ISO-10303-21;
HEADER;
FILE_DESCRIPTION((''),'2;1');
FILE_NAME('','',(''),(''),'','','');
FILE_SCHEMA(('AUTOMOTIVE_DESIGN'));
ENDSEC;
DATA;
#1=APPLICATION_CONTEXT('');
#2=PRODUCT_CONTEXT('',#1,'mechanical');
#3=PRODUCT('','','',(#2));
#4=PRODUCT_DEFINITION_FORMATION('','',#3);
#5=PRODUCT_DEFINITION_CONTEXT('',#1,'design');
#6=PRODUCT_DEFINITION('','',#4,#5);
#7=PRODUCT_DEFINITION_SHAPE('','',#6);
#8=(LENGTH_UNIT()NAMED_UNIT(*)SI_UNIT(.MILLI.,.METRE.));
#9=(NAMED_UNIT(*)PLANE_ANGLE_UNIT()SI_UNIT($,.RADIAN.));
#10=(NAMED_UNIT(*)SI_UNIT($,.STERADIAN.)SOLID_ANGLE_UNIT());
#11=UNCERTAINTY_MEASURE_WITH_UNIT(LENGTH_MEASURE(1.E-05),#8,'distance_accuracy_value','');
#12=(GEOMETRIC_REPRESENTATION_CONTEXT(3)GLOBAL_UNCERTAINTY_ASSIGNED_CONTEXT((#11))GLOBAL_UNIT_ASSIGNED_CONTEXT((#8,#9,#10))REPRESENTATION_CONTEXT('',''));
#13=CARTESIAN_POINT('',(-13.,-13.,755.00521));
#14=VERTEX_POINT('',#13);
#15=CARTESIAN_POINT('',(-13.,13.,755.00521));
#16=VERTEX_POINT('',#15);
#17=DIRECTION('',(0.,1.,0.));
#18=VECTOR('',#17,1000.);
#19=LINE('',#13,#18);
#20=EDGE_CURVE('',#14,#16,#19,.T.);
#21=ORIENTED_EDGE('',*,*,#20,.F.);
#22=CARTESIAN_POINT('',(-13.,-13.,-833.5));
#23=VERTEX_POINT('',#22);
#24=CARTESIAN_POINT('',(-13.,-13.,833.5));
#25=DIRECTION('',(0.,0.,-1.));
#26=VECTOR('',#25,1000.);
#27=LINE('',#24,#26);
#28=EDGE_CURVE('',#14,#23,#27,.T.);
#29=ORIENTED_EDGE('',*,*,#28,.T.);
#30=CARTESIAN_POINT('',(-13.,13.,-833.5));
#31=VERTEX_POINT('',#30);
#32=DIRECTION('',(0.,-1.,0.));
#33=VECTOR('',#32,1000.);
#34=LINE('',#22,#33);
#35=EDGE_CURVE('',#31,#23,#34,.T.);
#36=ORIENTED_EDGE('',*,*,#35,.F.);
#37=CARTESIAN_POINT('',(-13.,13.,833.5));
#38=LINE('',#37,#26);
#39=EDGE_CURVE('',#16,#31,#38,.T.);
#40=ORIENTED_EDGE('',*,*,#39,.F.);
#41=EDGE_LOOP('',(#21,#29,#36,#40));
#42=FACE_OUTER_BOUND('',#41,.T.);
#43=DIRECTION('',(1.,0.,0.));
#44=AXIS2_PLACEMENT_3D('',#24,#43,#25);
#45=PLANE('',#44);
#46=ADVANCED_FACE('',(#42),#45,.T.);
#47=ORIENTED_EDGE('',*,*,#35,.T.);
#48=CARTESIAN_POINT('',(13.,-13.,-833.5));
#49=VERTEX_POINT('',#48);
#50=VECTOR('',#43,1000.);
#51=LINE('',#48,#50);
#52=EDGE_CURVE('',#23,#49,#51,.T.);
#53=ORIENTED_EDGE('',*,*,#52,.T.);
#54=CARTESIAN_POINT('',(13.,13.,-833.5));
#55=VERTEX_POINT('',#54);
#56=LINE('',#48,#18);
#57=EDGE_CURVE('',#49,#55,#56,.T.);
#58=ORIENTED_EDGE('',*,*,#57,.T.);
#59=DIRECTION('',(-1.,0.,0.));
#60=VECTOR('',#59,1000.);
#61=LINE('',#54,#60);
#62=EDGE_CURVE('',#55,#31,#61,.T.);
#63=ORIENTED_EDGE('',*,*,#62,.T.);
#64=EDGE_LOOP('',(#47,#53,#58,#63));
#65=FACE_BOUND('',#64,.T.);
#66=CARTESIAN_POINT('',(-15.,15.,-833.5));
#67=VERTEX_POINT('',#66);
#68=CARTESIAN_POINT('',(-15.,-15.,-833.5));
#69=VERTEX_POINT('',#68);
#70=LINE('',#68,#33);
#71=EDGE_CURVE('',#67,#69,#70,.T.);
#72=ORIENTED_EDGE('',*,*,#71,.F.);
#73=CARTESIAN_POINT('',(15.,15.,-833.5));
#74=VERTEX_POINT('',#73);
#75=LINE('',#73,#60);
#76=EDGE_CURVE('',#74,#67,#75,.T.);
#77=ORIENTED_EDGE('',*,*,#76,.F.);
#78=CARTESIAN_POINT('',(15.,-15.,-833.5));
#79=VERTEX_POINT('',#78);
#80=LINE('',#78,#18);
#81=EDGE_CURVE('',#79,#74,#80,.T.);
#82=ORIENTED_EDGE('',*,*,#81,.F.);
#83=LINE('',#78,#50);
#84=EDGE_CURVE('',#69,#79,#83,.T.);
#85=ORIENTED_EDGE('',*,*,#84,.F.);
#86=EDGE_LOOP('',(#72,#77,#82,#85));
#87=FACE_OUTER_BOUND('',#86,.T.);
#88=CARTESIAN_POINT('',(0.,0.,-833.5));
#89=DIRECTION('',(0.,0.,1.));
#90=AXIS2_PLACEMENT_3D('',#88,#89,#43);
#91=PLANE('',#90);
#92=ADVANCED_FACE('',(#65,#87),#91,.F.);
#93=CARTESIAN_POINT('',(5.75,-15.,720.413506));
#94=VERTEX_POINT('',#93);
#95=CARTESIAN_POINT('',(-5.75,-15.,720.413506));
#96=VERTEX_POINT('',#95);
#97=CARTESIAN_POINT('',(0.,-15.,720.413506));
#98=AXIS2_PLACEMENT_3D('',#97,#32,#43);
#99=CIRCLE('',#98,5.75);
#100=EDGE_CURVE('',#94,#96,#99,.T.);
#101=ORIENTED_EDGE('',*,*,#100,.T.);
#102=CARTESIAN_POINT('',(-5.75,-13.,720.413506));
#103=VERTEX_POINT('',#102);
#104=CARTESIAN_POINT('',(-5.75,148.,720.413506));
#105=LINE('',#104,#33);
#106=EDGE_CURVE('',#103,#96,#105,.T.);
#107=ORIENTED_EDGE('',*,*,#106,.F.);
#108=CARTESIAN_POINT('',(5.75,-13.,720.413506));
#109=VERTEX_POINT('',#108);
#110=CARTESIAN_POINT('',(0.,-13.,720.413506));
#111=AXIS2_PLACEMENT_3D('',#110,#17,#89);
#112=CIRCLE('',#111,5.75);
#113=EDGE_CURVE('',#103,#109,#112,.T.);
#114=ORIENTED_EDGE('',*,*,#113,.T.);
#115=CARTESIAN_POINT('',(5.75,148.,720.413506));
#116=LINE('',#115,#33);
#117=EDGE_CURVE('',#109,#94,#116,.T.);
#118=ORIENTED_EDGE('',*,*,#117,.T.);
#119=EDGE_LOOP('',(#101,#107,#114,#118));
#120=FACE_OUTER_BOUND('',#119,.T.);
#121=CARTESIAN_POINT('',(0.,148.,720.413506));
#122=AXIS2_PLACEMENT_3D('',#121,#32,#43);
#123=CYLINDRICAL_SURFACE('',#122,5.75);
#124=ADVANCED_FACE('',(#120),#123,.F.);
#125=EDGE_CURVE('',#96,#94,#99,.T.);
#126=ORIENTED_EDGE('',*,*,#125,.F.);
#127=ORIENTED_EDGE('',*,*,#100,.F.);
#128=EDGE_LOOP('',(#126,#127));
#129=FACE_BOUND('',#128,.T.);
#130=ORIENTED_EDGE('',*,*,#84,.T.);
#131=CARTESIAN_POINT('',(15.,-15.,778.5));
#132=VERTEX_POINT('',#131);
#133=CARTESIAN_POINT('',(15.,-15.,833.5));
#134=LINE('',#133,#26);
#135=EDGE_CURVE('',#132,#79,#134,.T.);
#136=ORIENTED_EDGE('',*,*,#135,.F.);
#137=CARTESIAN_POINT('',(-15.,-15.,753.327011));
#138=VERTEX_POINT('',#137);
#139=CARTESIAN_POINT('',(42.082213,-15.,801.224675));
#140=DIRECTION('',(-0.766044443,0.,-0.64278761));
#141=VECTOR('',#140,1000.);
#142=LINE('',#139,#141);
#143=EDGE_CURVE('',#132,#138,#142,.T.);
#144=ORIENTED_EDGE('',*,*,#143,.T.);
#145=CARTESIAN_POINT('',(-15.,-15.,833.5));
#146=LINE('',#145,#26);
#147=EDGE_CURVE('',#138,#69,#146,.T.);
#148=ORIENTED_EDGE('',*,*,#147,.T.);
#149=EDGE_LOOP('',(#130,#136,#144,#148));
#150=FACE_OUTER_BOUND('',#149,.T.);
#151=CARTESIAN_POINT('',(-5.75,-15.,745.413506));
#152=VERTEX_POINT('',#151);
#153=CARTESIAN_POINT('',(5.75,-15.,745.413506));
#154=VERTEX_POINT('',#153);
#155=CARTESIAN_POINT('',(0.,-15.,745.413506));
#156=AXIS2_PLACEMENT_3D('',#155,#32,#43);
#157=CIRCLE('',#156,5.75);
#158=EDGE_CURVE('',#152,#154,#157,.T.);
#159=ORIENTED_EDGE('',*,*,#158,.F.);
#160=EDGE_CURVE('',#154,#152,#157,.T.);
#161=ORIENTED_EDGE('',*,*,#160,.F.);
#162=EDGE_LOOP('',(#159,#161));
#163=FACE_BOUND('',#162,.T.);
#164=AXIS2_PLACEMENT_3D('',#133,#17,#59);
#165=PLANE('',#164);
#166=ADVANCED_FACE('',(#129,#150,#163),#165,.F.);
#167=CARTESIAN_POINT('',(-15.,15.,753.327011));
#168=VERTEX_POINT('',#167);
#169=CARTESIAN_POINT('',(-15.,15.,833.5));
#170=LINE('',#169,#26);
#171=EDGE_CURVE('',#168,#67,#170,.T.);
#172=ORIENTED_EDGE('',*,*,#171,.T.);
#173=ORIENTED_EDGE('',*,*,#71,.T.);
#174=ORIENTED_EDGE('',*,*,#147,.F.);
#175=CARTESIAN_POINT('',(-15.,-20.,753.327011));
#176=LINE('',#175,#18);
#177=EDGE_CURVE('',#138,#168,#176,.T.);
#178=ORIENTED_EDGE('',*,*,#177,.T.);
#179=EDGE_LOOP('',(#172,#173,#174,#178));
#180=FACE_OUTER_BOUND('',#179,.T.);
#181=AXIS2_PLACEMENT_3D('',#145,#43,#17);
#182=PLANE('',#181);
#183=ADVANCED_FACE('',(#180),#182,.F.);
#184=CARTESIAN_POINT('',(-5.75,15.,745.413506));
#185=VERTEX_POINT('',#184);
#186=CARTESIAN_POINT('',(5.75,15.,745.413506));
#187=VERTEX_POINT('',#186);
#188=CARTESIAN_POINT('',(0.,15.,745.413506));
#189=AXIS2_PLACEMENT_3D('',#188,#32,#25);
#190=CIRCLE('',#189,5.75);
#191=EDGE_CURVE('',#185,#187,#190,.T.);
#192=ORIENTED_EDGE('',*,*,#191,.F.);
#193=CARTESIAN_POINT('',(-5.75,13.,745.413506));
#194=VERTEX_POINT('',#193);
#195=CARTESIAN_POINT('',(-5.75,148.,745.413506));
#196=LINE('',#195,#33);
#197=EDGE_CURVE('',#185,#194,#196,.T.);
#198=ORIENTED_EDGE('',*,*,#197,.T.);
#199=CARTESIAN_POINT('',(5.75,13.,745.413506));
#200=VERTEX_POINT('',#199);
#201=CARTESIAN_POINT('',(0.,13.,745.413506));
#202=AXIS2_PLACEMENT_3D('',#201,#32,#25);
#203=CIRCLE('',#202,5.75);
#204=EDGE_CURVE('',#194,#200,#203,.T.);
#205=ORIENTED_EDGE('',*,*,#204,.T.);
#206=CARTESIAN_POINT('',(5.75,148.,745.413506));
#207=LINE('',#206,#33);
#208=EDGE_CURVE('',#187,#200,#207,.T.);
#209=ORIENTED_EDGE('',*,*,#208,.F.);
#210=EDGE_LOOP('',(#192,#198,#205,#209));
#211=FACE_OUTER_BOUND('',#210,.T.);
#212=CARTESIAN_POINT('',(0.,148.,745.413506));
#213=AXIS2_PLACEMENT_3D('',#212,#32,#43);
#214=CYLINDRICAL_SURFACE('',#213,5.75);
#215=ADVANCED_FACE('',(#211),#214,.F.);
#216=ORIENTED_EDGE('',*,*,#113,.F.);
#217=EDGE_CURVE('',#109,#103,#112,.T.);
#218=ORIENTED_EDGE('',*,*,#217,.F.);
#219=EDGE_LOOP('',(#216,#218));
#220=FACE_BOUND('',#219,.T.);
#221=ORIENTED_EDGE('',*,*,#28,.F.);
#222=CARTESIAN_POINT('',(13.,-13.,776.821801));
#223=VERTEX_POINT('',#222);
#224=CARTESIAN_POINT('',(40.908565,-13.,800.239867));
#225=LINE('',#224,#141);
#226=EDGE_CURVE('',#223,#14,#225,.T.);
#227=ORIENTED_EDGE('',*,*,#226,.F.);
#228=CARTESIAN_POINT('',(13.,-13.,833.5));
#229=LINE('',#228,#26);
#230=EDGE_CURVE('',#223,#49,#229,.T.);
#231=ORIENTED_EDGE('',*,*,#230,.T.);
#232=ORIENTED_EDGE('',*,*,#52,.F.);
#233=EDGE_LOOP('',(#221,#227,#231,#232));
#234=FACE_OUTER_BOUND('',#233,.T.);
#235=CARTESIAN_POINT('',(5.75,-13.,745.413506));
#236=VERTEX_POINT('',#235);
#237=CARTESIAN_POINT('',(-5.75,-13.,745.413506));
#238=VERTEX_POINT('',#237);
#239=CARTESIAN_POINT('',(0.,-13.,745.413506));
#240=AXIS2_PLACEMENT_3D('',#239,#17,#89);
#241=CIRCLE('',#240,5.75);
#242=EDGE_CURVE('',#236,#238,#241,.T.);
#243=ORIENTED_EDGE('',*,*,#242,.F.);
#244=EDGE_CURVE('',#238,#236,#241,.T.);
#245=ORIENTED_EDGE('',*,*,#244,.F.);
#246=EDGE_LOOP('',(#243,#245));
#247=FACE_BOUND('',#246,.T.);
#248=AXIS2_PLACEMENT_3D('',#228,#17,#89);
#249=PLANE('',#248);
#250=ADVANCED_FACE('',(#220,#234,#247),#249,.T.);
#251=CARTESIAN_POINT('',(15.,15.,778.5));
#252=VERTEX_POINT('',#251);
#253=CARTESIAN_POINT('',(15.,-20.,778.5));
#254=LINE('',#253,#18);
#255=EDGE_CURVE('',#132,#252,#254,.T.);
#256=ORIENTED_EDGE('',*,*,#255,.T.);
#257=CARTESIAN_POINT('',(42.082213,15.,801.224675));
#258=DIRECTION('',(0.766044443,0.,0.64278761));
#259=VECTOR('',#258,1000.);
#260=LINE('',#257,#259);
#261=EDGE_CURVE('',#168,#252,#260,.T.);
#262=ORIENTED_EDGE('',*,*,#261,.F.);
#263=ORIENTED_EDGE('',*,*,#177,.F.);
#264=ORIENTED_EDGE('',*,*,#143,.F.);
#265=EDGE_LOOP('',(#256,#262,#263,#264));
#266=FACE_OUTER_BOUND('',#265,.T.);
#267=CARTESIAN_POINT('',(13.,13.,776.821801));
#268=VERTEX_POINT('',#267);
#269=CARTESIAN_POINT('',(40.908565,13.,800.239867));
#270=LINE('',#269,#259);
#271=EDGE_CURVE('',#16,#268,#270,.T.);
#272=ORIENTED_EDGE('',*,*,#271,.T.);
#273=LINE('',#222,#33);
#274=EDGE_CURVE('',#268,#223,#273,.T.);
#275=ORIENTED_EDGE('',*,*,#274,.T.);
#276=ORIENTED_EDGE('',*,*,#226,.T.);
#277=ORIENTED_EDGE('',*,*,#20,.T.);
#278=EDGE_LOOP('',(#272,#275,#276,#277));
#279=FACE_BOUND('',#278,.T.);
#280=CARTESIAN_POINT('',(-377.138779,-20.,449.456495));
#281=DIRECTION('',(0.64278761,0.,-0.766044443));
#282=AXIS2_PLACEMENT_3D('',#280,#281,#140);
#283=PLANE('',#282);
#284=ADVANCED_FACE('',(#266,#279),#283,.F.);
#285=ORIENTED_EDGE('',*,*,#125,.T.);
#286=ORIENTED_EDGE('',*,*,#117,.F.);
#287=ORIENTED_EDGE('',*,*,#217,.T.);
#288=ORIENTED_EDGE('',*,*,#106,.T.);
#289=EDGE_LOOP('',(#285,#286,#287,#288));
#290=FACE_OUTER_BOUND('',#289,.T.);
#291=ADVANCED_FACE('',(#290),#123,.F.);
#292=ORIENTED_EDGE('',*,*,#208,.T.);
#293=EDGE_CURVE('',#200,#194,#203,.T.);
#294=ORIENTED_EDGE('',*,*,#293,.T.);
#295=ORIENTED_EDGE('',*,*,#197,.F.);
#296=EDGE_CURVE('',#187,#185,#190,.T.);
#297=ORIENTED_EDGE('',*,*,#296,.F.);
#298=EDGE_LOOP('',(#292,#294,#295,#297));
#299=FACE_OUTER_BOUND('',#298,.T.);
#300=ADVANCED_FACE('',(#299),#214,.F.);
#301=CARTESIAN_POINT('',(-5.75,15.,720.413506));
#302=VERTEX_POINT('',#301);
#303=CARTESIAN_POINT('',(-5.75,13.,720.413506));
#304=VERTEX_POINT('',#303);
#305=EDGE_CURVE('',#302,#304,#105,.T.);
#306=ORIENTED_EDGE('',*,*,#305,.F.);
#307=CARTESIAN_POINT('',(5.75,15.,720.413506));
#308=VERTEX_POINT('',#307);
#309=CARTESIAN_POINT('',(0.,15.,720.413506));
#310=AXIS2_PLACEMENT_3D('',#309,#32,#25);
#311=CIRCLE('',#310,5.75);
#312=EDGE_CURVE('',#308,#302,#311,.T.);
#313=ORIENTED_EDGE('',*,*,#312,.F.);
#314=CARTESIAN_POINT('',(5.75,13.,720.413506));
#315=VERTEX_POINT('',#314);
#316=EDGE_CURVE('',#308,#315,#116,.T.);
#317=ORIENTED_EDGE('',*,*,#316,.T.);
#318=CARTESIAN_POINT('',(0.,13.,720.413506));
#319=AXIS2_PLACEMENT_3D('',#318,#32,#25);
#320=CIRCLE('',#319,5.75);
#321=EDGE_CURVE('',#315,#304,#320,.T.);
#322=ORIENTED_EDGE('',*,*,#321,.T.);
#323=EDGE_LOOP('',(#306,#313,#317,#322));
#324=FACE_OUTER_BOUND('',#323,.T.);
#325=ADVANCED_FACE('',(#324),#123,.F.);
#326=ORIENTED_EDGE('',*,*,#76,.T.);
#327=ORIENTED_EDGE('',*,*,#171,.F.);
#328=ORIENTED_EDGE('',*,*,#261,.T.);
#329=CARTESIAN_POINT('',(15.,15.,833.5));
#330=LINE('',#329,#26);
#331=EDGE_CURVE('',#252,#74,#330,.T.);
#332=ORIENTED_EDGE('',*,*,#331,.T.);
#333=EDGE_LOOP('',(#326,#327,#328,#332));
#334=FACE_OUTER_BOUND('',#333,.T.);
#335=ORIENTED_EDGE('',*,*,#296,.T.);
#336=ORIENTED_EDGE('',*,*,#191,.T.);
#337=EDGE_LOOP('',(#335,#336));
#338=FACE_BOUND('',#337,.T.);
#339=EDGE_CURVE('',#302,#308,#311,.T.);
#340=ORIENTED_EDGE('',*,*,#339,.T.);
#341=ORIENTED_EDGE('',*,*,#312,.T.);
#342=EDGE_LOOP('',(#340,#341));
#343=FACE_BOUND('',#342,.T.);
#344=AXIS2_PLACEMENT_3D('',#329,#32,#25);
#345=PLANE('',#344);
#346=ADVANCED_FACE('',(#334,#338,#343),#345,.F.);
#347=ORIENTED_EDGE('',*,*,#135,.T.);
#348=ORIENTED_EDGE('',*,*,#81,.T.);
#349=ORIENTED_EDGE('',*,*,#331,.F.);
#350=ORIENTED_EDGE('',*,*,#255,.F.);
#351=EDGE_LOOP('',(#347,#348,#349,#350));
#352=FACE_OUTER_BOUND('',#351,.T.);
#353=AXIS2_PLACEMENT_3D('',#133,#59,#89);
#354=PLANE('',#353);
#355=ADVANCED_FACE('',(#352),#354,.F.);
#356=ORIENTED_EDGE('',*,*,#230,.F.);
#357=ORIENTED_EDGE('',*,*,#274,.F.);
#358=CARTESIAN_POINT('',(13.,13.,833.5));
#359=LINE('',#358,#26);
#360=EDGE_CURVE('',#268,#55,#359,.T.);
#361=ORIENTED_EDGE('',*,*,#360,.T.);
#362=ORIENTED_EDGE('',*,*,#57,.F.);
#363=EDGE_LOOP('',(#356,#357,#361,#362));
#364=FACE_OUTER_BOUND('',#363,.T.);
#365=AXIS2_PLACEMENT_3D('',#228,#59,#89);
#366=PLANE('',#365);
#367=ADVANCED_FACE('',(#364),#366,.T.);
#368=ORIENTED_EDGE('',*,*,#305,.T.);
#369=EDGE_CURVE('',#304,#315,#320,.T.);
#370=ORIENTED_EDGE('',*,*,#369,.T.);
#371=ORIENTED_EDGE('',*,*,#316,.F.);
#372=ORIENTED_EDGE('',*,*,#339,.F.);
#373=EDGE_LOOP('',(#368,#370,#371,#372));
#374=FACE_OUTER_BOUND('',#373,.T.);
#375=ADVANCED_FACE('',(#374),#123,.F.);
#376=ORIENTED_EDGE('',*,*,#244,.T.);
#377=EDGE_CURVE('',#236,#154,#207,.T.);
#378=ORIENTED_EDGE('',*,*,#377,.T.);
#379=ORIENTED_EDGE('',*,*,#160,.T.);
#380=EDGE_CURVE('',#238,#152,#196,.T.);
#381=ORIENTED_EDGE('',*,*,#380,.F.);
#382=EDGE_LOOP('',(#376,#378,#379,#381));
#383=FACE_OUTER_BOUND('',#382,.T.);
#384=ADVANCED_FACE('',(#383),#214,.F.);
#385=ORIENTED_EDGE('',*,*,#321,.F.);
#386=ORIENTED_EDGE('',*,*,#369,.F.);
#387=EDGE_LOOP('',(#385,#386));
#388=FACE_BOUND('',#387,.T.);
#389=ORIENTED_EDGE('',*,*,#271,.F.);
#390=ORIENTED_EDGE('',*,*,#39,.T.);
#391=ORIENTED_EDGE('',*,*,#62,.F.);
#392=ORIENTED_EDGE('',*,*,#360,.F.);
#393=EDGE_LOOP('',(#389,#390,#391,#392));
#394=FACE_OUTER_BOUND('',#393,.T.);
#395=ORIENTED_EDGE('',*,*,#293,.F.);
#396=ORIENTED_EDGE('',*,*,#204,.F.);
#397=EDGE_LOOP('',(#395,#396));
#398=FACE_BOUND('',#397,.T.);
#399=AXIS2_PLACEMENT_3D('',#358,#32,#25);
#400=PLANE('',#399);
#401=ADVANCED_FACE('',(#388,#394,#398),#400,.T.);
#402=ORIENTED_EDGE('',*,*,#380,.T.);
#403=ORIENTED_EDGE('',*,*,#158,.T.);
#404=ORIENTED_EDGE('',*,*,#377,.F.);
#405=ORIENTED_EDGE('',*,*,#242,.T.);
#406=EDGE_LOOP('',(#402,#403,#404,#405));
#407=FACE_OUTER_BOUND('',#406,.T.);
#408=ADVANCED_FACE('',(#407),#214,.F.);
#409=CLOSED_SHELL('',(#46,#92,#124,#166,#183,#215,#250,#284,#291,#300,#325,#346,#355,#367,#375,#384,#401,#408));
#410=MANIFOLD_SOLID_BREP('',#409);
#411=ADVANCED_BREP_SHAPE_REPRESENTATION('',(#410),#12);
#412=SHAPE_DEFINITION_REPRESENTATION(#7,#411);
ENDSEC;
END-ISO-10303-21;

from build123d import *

# Parameters (mm, degrees)
SKETCH_1_W          = 30
SKETCH_1_H          = 30
SKETCH_1_W_2        = 26
SKETCH_1_H_2        = 26
EXTRUDE_1_DEPTH     = 833.5
CUT_EXTRUDE_1_DEPTH = 35
SKETCH_4_R          = 5.75
CUT_EXTRUDE_2_DEPTH = 163


with BuildPart() as part:
    # 草图1 → 凸台-拉伸1 (new, symmetric)
    with BuildSketch(Plane.XY):
        Rectangle(SKETCH_1_W, SKETCH_1_H)
        Rectangle(SKETCH_1_W_2, SKETCH_1_H_2, mode=Mode.SUBTRACT)
    extrude(amount=EXTRUDE_1_DEPTH, both=True)

    # 草图3 → 切除-拉伸1 (cut, symmetric)
    with BuildSketch(Plane(origin=(0, 15, 0), x_dir=(1, 0, 0), z_dir=(0, 1, 0))):
        Polygon((15, -833.5), (15, -778.5), (-15, -753.327011065), (-15, -833.5), align=None)
    extrude(amount=CUT_EXTRUDE_1_DEPTH, both=True, mode=Mode.SUBTRACT)

    # 草图4 → 切除-拉伸2 (cut)
    with BuildSketch(Plane.XZ.offset(15)):
        with Locations((0, 745.413505532)):
            Circle(SKETCH_4_R)
        with Locations((0, 720.413505532)):
            Circle(SKETCH_4_R)
    extrude(amount=-CUT_EXTRUDE_2_DEPTH, mode=Mode.SUBTRACT)


solid = part.part
